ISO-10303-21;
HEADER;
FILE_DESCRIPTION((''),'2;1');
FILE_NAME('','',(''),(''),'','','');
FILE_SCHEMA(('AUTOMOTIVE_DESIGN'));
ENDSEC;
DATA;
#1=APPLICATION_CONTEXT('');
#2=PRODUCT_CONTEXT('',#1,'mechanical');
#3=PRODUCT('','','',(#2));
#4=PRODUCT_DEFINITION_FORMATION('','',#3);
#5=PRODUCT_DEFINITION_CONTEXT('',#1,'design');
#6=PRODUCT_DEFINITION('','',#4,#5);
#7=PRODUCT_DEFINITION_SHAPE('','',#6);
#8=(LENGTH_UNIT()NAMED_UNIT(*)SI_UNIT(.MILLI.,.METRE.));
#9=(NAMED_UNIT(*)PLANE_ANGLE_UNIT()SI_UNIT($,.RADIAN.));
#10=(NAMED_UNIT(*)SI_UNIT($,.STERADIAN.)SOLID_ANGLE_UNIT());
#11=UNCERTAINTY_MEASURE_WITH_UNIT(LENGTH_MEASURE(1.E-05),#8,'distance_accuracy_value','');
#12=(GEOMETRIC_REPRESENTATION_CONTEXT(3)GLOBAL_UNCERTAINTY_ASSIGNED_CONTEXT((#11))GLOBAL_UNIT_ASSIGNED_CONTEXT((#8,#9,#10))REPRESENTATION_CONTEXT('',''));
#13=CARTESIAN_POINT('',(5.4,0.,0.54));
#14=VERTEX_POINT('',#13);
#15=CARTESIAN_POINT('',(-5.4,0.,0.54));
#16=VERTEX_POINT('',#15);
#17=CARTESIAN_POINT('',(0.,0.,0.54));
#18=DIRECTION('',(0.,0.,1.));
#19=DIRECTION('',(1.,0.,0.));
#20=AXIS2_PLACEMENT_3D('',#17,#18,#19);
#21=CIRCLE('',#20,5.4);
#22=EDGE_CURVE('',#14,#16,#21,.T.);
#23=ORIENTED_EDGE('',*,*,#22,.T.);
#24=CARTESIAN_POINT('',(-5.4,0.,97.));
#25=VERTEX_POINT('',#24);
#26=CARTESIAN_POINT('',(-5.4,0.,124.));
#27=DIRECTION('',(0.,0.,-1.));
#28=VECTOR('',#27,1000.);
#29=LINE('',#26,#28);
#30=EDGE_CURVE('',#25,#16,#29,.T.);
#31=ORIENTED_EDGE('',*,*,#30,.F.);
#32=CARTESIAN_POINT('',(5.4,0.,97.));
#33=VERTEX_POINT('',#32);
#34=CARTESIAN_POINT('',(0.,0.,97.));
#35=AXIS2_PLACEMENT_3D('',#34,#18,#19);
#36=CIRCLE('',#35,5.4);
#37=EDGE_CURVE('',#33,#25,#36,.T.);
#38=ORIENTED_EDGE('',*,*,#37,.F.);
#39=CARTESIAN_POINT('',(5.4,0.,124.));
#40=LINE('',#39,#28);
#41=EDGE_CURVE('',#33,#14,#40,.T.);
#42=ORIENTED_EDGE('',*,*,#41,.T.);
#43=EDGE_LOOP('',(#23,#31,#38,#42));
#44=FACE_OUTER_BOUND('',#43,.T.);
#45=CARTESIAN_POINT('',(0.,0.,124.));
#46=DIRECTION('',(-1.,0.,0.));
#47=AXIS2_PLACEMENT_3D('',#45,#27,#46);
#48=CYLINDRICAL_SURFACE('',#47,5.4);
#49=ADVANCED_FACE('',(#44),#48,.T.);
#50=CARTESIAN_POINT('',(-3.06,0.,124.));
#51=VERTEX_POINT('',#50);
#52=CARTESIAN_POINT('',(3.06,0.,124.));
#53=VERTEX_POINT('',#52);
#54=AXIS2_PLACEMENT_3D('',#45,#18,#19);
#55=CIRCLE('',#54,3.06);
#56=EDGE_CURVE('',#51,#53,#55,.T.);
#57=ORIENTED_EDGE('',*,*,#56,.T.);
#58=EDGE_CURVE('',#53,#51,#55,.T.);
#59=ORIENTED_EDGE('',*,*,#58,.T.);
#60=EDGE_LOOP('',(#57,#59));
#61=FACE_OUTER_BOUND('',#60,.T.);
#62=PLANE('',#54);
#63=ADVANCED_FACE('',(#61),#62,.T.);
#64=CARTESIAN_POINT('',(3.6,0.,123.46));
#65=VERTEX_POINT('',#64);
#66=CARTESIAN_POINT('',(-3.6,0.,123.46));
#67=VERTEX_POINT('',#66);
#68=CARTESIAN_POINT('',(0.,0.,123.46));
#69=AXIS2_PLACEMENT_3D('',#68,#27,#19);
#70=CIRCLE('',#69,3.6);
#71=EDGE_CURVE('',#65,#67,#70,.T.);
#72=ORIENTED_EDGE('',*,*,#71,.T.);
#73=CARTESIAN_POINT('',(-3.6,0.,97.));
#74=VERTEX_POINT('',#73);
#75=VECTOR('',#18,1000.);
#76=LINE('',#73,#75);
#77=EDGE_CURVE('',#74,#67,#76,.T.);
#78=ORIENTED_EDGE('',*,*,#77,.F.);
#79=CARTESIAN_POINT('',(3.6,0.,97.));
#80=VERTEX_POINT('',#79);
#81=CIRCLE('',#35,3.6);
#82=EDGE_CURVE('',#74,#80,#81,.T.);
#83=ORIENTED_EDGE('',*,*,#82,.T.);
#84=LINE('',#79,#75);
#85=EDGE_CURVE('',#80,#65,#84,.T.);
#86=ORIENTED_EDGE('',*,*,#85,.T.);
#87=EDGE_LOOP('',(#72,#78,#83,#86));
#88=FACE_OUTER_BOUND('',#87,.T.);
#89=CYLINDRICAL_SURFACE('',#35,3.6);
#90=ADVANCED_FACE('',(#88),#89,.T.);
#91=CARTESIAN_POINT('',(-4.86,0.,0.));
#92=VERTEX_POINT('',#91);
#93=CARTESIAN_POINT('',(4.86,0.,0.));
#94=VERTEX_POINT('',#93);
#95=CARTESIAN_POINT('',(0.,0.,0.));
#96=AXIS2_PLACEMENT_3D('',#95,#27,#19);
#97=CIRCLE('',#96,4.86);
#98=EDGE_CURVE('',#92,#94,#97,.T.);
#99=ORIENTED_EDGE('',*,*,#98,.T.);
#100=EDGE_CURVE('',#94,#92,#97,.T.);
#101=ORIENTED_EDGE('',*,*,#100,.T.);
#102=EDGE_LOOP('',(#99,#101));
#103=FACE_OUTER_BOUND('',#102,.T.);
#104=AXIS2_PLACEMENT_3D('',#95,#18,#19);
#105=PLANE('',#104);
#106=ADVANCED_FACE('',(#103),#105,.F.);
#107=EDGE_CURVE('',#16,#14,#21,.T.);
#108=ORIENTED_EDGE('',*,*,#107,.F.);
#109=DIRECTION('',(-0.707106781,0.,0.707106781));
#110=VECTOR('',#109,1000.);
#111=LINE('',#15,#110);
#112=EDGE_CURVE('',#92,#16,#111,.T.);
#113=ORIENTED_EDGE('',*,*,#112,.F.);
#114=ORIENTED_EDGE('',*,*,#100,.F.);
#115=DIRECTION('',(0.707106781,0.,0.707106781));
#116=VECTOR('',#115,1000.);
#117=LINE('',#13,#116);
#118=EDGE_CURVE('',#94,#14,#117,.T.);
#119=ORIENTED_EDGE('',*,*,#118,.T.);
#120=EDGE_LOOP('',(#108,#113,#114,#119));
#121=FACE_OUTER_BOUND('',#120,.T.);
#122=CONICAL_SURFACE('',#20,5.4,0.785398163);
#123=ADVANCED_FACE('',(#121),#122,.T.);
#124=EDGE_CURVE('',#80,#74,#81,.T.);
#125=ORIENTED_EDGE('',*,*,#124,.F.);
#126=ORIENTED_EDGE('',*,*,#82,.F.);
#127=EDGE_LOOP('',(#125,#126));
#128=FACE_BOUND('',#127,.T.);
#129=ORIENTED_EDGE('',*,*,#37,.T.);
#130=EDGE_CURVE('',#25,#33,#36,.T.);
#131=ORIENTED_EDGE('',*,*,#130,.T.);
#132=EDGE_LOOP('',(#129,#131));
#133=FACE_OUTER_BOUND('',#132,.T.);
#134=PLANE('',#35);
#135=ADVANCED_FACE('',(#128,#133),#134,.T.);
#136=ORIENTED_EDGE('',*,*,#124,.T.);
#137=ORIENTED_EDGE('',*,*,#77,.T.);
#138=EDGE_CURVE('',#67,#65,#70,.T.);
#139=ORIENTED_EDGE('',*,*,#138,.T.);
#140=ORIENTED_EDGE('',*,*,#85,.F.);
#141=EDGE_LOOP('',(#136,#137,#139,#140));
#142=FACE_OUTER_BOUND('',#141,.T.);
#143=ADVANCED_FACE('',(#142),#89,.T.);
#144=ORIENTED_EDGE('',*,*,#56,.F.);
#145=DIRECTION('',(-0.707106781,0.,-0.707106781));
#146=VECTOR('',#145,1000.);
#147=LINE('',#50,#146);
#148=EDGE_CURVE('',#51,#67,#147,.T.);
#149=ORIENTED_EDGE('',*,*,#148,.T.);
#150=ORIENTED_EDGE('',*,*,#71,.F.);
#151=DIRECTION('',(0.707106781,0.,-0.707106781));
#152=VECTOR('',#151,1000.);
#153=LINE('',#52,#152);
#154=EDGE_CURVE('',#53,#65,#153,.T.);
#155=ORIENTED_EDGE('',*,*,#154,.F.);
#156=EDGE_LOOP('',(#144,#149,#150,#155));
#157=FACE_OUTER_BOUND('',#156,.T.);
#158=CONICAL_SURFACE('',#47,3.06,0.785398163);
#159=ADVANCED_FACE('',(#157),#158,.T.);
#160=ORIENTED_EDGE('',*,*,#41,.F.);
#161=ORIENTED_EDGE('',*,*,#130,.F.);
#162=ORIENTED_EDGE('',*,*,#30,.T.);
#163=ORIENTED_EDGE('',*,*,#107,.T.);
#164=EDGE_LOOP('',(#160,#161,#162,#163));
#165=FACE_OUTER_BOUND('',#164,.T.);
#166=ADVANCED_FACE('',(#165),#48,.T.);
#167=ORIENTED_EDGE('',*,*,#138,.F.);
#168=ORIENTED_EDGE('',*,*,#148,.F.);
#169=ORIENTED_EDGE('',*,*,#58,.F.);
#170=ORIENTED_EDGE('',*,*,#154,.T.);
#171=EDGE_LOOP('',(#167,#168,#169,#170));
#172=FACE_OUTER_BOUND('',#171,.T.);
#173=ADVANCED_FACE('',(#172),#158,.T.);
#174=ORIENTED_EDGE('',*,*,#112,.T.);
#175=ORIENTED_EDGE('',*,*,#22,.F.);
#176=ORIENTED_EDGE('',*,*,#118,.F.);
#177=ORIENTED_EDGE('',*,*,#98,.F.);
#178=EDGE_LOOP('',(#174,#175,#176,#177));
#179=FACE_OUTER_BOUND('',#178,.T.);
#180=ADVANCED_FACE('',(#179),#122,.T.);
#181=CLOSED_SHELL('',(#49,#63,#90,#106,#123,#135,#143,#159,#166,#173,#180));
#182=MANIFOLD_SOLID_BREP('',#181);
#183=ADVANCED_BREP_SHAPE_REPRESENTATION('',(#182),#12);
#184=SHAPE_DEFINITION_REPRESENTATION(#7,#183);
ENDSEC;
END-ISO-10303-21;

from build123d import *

# Parameters (mm, degrees)
SKETCH1_R           = 5.4
BOSS_EXTRUDE1_DEPTH = 124
CUT_EXTRUDE1_START  = -27
SKETCH2_R           = 5.4
SKETCH2_R_2         = 3.6
CUT_EXTRUDE1_DEPTH  = 27
CHAMFER1_SIZE       = 0.54


with BuildPart() as part:
    # Sketch1 → Boss-Extrude1 (new body)
    with BuildSketch(Plane.XY):
        Circle(SKETCH1_R)
    extrude(amount=BOSS_EXTRUDE1_DEPTH)

    # Sketch2 → Cut-Extrude1 (cut)
    with BuildSketch(Plane.XY.offset(124).offset(CUT_EXTRUDE1_START)):
        Circle(SKETCH2_R)
        Circle(SKETCH2_R_2, mode=Mode.SUBTRACT)
    extrude(amount=CUT_EXTRUDE1_DEPTH, mode=Mode.SUBTRACT)

    # Chamfer1
    chamfer1_edges = [part.edges().sort_by_distance(p)[0] for p in [
        (-5.4, 0, 0),
        (-3.6, 0, 124),
    ]]
    chamfer(chamfer1_edges, length=CHAMFER1_SIZE)


solid = part.part
